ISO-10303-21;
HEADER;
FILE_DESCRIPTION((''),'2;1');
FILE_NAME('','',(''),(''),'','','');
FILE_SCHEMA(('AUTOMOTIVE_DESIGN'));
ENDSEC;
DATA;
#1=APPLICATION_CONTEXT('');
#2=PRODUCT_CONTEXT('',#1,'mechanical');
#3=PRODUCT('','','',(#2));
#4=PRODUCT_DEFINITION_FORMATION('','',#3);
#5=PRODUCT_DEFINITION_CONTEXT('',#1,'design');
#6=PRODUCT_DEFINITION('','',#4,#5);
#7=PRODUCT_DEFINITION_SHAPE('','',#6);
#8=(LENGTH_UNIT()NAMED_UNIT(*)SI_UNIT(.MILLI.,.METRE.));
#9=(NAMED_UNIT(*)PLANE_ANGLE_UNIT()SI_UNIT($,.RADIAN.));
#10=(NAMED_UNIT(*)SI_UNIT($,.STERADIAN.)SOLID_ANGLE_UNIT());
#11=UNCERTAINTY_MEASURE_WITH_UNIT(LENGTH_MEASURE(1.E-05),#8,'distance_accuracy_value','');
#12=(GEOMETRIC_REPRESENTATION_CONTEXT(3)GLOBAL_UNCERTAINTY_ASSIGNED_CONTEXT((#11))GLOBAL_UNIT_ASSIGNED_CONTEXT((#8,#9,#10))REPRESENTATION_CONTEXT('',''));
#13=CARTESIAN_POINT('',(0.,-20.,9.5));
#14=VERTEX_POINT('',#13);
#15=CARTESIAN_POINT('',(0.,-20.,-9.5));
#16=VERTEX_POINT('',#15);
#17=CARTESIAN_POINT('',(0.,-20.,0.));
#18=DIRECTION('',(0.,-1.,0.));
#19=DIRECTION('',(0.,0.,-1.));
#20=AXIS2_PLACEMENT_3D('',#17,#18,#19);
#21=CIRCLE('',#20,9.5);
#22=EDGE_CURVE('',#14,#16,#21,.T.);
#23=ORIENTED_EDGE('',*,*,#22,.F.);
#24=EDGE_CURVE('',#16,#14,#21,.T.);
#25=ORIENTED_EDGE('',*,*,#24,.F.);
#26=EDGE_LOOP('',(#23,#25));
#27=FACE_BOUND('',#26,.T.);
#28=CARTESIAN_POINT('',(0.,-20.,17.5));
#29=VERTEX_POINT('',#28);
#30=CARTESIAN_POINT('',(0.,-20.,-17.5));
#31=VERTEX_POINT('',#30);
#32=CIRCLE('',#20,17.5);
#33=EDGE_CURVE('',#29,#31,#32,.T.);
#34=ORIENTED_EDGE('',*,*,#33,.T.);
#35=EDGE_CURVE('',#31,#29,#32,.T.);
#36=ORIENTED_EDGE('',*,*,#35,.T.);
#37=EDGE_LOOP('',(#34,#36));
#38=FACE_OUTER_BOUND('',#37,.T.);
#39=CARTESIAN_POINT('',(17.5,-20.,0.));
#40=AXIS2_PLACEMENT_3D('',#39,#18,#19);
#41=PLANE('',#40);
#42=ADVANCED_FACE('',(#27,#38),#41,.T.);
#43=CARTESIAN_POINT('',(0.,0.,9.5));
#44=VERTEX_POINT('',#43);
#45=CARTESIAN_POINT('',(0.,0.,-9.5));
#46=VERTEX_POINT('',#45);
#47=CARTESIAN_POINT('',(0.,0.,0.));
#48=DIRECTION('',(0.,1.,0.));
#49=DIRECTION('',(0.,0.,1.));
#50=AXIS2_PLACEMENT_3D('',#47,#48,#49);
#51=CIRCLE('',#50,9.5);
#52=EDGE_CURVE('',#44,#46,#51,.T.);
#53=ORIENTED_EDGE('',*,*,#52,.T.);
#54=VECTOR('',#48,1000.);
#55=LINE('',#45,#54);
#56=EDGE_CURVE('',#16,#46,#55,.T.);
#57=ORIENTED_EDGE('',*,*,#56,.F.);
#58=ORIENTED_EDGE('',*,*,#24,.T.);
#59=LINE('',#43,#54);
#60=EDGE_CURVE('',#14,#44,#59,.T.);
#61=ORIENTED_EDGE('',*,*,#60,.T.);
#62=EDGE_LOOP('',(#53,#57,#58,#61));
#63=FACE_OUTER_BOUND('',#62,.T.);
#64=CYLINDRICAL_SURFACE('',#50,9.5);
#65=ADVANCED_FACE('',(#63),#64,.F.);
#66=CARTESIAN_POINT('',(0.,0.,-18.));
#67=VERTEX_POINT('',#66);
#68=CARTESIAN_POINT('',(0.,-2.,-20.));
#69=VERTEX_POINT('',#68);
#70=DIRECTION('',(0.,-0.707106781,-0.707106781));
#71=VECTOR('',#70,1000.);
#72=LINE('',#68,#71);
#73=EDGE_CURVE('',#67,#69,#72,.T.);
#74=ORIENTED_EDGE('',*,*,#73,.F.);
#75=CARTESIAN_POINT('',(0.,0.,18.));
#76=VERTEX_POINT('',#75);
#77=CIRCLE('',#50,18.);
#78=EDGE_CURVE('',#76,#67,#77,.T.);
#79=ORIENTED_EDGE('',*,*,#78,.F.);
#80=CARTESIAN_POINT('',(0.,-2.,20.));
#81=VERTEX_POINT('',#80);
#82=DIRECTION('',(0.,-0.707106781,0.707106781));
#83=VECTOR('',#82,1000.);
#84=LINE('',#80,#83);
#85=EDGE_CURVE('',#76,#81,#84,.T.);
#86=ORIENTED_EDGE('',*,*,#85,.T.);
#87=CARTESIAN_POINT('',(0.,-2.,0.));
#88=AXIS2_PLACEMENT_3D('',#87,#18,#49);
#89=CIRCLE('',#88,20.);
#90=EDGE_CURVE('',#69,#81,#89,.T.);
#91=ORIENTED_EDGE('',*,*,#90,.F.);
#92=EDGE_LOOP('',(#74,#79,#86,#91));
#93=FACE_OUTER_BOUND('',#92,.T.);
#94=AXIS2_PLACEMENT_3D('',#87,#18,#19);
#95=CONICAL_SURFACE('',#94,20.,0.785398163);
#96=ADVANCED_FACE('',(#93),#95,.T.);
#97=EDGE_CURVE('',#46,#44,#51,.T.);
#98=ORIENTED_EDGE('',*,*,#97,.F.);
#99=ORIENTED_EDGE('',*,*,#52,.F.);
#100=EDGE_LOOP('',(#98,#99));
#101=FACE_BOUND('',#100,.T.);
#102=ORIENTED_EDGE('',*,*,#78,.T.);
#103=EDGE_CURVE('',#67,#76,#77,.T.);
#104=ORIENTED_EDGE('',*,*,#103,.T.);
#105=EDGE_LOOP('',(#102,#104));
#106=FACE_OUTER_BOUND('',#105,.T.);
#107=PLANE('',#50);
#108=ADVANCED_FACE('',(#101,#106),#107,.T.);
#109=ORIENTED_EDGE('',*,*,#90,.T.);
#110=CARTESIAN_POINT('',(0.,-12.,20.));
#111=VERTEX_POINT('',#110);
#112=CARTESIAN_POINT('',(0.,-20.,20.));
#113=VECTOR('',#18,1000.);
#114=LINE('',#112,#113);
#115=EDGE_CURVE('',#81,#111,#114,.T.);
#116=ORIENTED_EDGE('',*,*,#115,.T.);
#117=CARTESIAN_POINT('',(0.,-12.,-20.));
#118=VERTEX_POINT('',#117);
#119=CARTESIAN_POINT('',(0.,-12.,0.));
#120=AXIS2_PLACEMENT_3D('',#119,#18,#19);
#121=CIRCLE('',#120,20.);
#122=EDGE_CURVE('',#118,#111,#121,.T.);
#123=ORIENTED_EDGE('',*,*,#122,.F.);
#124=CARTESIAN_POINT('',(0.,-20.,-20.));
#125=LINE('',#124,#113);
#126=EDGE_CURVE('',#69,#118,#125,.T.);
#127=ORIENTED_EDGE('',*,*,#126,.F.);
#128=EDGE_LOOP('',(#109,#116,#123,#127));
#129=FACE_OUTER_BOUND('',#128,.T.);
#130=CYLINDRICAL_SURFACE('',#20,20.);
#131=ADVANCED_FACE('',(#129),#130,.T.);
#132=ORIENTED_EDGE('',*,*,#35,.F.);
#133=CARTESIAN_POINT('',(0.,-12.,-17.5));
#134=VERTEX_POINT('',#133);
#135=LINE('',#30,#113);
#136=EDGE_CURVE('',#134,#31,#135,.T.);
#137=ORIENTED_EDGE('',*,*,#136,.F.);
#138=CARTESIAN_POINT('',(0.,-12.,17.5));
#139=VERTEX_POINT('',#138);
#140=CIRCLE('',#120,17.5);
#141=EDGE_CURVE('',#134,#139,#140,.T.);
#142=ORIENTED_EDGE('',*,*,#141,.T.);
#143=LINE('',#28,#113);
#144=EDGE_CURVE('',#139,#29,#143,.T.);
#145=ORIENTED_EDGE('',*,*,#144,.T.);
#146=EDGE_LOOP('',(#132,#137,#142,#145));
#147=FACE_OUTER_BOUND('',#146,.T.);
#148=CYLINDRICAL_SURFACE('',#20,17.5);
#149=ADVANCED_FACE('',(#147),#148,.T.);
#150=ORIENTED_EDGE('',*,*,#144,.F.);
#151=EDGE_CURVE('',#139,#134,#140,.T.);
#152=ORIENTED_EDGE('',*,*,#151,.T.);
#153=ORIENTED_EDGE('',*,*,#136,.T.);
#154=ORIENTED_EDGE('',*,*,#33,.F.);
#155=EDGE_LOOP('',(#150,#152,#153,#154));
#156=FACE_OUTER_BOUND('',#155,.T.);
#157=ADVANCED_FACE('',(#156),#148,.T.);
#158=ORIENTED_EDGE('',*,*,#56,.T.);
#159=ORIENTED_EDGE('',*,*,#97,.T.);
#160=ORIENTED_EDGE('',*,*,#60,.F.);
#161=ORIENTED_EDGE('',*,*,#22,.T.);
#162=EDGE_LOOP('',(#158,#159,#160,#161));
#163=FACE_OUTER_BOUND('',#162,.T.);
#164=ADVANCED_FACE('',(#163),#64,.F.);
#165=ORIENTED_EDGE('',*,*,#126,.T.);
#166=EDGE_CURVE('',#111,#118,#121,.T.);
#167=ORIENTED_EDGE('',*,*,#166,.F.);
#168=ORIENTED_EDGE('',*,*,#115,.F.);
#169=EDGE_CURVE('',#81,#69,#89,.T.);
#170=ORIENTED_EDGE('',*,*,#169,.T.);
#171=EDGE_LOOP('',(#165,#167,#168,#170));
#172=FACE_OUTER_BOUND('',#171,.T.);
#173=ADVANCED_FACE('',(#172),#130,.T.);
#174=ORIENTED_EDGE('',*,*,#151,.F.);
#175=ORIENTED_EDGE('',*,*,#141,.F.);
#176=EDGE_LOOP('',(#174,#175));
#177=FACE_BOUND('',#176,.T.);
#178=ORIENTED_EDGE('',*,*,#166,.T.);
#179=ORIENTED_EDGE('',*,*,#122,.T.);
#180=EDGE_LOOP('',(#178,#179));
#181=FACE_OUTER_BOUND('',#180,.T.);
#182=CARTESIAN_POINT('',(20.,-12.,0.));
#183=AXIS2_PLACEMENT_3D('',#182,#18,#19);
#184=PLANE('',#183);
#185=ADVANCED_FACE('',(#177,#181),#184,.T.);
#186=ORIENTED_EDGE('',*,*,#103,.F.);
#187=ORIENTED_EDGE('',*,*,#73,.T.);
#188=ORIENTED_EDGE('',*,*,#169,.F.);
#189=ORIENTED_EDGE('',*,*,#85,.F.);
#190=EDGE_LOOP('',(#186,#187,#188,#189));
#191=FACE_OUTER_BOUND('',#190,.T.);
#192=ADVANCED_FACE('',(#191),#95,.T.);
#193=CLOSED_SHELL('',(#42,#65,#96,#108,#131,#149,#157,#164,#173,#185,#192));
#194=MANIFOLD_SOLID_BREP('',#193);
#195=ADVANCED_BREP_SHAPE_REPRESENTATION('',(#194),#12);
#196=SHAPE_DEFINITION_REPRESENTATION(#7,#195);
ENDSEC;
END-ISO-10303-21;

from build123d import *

# Parameters (mm, degrees)
G1_2_TAPPED_HOLE1_D     = 19
G1_2_TAPPED_HOLE1_DEPTH = 47.35
G1_2_TAPPED_HOLE1_TIP   = 5.708175881
CHAMFER1_SIZE           = 2


with BuildPart() as part:
    # Sketch1 → Revolve1 (revolve)
    with BuildSketch(Plane.XY, mode=Mode.PRIVATE) as revolve1_sk:
        Polygon((0, 0), (20, 0), (20, -12), (17.5, -12), (17.5, -20), (0, -20), align=None)
    revolve(revolve1_sk.sketch.rotate(Axis((0, -20, 0), (0, 1, 0)), 90), axis=Axis((0, -20, 0), (0, 1, 0)))

    # G1/2 Tapped Hole1
    with Locations(Plane(origin=(0, 0, 0), x_dir=(1, 0, 0), z_dir=(0, 1, 0))):
        with Locations((0, 0)):
            Hole(G1_2_TAPPED_HOLE1_D / 2, depth=G1_2_TAPPED_HOLE1_DEPTH)
            with Locations((0, 0, -(G1_2_TAPPED_HOLE1_DEPTH + G1_2_TAPPED_HOLE1_TIP / 2))):  # 118° drill point
                Cone(0, G1_2_TAPPED_HOLE1_D / 2, G1_2_TAPPED_HOLE1_TIP, mode=Mode.SUBTRACT)

    # Chamfer1
    chamfer1_edges = [part.edges().sort_by_distance(p)[0] for p in [
        (0, 0, 20),
    ]]
    chamfer(chamfer1_edges, length=CHAMFER1_SIZE)


solid = part.part
